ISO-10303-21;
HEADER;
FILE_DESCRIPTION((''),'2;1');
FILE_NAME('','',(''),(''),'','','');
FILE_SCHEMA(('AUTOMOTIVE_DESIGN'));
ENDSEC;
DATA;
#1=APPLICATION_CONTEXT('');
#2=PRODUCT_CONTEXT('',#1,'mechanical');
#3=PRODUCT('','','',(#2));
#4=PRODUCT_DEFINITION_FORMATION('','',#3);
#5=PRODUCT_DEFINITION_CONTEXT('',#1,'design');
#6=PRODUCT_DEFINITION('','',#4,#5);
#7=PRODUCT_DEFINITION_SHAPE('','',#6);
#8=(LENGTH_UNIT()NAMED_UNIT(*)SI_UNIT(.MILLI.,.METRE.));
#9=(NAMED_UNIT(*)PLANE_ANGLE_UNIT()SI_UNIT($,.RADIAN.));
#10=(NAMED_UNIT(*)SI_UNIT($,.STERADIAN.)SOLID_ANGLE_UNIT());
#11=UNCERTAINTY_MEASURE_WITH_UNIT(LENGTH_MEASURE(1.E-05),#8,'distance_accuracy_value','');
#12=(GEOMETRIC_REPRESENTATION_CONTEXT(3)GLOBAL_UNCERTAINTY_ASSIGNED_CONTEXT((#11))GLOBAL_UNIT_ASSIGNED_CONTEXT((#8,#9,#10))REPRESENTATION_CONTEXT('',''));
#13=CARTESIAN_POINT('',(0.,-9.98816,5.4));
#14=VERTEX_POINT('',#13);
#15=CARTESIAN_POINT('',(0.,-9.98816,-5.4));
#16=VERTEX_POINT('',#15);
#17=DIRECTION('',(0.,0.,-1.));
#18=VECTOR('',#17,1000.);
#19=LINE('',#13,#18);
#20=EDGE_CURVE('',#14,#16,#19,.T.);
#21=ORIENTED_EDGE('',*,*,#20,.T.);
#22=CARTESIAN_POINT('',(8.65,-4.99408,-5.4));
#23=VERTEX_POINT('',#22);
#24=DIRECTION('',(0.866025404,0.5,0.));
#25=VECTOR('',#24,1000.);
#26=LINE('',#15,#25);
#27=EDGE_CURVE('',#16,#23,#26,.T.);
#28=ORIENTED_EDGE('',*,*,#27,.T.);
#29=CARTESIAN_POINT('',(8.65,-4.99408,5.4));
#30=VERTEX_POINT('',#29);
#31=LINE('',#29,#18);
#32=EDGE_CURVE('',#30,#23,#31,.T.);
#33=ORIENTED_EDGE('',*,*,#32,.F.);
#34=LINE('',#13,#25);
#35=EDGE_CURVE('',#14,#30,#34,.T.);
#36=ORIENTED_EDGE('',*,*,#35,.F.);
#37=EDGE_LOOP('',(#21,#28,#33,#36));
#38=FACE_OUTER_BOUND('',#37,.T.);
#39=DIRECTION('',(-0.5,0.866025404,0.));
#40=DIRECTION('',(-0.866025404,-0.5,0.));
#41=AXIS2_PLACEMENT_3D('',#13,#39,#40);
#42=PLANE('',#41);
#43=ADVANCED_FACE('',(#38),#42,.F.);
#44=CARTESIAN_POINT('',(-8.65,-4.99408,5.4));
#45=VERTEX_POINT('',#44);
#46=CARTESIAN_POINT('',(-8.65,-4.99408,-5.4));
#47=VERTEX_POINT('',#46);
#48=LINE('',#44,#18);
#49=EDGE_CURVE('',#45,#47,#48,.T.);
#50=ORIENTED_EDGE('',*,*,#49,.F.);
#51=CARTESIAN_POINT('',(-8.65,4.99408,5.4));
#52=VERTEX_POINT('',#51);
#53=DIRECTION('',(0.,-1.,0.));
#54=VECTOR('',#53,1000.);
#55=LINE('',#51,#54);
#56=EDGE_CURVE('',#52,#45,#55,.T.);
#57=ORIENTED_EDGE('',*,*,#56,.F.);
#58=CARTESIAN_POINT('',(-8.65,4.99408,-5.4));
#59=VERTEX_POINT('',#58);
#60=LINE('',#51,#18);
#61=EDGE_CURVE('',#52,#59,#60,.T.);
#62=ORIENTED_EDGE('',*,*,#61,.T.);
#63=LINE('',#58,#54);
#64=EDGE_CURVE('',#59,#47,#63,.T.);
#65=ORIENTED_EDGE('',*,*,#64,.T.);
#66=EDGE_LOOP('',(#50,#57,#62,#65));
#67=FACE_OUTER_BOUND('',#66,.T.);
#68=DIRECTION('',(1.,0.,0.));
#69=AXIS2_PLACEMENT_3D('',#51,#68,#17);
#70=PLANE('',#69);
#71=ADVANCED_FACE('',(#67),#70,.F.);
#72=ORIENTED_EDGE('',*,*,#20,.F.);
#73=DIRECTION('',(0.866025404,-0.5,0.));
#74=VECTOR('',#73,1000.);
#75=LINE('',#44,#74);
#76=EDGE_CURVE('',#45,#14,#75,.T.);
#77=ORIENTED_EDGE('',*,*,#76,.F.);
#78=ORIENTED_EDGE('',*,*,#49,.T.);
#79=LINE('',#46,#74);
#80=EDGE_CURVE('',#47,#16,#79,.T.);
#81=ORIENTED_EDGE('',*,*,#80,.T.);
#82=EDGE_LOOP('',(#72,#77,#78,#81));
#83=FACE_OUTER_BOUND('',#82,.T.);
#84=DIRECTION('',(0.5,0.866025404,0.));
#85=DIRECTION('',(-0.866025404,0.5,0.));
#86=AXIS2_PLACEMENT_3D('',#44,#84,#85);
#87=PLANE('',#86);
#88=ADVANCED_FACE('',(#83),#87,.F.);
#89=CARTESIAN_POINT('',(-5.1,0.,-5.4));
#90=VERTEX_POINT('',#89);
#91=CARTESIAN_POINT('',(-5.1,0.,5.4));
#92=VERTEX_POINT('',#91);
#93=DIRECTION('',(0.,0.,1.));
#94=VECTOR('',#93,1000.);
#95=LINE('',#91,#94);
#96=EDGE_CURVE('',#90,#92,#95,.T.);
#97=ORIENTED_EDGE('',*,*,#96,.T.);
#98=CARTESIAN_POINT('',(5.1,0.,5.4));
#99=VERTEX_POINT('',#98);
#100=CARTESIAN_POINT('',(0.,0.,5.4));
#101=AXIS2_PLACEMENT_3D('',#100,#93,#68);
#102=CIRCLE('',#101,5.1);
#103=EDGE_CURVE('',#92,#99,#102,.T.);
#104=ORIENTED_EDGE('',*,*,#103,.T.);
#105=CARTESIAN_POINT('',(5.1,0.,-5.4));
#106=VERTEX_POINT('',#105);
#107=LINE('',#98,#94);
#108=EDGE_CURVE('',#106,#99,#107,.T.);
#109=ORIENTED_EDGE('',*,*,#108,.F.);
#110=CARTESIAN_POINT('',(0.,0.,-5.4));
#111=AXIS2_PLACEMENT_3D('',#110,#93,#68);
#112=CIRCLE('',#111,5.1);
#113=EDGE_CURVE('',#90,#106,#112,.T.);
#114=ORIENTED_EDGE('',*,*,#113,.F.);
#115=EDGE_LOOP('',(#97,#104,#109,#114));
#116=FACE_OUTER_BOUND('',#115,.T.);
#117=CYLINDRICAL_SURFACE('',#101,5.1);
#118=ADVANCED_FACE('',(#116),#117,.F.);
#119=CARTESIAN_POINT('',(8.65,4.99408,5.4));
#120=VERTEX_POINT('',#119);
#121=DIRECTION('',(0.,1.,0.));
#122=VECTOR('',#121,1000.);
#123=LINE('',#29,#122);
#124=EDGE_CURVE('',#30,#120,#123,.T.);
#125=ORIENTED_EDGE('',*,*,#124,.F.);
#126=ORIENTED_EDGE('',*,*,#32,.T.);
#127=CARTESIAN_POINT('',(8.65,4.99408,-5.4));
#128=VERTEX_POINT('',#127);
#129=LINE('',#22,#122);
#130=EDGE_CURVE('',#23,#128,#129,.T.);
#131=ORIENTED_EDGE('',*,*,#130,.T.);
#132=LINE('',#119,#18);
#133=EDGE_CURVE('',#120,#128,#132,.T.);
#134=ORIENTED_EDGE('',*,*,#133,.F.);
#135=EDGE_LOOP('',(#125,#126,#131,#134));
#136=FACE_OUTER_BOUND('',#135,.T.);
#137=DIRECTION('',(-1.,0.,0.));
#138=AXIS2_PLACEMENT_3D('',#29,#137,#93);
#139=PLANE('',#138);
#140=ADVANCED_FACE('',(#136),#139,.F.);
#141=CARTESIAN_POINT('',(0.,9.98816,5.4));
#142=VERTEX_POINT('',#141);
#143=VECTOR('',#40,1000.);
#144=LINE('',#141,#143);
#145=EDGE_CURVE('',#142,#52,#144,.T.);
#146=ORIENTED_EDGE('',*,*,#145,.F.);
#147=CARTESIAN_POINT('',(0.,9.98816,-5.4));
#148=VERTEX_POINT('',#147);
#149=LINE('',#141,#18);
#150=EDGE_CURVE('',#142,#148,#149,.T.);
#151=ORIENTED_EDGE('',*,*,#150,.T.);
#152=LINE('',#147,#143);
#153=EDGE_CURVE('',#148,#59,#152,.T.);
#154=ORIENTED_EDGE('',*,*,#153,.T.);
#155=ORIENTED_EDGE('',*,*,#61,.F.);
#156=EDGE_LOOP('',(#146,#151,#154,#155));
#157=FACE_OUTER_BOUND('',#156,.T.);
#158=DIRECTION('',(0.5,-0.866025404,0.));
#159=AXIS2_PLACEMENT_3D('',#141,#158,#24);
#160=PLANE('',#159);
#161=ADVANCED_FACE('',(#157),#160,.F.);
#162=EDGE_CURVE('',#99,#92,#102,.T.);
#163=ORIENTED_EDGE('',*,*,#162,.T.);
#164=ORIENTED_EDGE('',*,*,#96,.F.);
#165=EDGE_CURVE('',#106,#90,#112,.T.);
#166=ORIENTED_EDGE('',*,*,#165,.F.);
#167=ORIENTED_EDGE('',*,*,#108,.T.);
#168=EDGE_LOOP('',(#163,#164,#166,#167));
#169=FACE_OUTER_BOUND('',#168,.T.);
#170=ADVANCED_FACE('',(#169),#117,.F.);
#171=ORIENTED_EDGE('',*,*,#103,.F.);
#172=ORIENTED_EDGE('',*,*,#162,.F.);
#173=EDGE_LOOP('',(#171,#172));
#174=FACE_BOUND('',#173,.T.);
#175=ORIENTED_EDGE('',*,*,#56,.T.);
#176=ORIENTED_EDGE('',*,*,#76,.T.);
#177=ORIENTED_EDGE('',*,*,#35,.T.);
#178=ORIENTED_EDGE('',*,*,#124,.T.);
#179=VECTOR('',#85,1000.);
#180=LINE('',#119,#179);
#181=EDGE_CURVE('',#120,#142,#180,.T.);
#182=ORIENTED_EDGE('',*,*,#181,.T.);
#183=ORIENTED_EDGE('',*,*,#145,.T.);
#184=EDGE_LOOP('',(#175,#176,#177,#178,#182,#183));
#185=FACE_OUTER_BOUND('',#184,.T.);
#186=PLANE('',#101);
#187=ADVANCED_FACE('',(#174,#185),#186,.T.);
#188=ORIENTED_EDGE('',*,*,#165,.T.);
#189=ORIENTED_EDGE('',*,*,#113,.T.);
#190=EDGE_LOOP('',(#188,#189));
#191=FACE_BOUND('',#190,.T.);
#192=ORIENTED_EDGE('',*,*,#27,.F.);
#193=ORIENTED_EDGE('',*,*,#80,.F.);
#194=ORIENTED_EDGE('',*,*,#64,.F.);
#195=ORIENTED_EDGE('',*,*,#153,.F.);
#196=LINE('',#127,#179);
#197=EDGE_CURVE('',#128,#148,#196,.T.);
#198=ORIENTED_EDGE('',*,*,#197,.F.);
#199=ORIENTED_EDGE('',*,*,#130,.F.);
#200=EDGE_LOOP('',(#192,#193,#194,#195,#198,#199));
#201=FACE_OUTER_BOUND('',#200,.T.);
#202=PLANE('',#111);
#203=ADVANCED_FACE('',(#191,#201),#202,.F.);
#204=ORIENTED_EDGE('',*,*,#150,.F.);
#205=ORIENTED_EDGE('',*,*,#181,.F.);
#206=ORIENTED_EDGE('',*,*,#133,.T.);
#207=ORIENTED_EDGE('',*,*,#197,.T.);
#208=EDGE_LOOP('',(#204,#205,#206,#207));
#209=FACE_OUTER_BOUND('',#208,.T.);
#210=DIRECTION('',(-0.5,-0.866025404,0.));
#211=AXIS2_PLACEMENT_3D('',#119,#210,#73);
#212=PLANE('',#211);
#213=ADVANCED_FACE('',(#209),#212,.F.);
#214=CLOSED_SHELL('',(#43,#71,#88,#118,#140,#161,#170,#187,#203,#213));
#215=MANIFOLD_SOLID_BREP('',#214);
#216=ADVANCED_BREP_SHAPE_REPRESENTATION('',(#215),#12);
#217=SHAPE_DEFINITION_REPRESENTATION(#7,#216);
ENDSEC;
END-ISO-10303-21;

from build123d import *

# Parameters (mm, degrees)
BOSS_EXTRUDE1_DEPTH = 5.4
M12_TAPPED_HOLE1_D  = 10.2


with BuildPart() as part:
    # Sketch1 → Boss-Extrude1 (new, symmetric)
    with BuildSketch(Plane.XY):
        Polygon((8.65, -4.994079828), (8.65, 4.994079828), (0, 9.988159657), (-8.65, 4.994079828), (-8.65, -4.994079828), (0, -9.988159657), align=None)
    extrude(amount=BOSS_EXTRUDE1_DEPTH, both=True)

    # M12 Tapped Hole1 (through all)
    with Locations(Plane.XY.offset(5.4)):
        with Locations((0, 0)):
            Hole(M12_TAPPED_HOLE1_D / 2)


solid = part.part
